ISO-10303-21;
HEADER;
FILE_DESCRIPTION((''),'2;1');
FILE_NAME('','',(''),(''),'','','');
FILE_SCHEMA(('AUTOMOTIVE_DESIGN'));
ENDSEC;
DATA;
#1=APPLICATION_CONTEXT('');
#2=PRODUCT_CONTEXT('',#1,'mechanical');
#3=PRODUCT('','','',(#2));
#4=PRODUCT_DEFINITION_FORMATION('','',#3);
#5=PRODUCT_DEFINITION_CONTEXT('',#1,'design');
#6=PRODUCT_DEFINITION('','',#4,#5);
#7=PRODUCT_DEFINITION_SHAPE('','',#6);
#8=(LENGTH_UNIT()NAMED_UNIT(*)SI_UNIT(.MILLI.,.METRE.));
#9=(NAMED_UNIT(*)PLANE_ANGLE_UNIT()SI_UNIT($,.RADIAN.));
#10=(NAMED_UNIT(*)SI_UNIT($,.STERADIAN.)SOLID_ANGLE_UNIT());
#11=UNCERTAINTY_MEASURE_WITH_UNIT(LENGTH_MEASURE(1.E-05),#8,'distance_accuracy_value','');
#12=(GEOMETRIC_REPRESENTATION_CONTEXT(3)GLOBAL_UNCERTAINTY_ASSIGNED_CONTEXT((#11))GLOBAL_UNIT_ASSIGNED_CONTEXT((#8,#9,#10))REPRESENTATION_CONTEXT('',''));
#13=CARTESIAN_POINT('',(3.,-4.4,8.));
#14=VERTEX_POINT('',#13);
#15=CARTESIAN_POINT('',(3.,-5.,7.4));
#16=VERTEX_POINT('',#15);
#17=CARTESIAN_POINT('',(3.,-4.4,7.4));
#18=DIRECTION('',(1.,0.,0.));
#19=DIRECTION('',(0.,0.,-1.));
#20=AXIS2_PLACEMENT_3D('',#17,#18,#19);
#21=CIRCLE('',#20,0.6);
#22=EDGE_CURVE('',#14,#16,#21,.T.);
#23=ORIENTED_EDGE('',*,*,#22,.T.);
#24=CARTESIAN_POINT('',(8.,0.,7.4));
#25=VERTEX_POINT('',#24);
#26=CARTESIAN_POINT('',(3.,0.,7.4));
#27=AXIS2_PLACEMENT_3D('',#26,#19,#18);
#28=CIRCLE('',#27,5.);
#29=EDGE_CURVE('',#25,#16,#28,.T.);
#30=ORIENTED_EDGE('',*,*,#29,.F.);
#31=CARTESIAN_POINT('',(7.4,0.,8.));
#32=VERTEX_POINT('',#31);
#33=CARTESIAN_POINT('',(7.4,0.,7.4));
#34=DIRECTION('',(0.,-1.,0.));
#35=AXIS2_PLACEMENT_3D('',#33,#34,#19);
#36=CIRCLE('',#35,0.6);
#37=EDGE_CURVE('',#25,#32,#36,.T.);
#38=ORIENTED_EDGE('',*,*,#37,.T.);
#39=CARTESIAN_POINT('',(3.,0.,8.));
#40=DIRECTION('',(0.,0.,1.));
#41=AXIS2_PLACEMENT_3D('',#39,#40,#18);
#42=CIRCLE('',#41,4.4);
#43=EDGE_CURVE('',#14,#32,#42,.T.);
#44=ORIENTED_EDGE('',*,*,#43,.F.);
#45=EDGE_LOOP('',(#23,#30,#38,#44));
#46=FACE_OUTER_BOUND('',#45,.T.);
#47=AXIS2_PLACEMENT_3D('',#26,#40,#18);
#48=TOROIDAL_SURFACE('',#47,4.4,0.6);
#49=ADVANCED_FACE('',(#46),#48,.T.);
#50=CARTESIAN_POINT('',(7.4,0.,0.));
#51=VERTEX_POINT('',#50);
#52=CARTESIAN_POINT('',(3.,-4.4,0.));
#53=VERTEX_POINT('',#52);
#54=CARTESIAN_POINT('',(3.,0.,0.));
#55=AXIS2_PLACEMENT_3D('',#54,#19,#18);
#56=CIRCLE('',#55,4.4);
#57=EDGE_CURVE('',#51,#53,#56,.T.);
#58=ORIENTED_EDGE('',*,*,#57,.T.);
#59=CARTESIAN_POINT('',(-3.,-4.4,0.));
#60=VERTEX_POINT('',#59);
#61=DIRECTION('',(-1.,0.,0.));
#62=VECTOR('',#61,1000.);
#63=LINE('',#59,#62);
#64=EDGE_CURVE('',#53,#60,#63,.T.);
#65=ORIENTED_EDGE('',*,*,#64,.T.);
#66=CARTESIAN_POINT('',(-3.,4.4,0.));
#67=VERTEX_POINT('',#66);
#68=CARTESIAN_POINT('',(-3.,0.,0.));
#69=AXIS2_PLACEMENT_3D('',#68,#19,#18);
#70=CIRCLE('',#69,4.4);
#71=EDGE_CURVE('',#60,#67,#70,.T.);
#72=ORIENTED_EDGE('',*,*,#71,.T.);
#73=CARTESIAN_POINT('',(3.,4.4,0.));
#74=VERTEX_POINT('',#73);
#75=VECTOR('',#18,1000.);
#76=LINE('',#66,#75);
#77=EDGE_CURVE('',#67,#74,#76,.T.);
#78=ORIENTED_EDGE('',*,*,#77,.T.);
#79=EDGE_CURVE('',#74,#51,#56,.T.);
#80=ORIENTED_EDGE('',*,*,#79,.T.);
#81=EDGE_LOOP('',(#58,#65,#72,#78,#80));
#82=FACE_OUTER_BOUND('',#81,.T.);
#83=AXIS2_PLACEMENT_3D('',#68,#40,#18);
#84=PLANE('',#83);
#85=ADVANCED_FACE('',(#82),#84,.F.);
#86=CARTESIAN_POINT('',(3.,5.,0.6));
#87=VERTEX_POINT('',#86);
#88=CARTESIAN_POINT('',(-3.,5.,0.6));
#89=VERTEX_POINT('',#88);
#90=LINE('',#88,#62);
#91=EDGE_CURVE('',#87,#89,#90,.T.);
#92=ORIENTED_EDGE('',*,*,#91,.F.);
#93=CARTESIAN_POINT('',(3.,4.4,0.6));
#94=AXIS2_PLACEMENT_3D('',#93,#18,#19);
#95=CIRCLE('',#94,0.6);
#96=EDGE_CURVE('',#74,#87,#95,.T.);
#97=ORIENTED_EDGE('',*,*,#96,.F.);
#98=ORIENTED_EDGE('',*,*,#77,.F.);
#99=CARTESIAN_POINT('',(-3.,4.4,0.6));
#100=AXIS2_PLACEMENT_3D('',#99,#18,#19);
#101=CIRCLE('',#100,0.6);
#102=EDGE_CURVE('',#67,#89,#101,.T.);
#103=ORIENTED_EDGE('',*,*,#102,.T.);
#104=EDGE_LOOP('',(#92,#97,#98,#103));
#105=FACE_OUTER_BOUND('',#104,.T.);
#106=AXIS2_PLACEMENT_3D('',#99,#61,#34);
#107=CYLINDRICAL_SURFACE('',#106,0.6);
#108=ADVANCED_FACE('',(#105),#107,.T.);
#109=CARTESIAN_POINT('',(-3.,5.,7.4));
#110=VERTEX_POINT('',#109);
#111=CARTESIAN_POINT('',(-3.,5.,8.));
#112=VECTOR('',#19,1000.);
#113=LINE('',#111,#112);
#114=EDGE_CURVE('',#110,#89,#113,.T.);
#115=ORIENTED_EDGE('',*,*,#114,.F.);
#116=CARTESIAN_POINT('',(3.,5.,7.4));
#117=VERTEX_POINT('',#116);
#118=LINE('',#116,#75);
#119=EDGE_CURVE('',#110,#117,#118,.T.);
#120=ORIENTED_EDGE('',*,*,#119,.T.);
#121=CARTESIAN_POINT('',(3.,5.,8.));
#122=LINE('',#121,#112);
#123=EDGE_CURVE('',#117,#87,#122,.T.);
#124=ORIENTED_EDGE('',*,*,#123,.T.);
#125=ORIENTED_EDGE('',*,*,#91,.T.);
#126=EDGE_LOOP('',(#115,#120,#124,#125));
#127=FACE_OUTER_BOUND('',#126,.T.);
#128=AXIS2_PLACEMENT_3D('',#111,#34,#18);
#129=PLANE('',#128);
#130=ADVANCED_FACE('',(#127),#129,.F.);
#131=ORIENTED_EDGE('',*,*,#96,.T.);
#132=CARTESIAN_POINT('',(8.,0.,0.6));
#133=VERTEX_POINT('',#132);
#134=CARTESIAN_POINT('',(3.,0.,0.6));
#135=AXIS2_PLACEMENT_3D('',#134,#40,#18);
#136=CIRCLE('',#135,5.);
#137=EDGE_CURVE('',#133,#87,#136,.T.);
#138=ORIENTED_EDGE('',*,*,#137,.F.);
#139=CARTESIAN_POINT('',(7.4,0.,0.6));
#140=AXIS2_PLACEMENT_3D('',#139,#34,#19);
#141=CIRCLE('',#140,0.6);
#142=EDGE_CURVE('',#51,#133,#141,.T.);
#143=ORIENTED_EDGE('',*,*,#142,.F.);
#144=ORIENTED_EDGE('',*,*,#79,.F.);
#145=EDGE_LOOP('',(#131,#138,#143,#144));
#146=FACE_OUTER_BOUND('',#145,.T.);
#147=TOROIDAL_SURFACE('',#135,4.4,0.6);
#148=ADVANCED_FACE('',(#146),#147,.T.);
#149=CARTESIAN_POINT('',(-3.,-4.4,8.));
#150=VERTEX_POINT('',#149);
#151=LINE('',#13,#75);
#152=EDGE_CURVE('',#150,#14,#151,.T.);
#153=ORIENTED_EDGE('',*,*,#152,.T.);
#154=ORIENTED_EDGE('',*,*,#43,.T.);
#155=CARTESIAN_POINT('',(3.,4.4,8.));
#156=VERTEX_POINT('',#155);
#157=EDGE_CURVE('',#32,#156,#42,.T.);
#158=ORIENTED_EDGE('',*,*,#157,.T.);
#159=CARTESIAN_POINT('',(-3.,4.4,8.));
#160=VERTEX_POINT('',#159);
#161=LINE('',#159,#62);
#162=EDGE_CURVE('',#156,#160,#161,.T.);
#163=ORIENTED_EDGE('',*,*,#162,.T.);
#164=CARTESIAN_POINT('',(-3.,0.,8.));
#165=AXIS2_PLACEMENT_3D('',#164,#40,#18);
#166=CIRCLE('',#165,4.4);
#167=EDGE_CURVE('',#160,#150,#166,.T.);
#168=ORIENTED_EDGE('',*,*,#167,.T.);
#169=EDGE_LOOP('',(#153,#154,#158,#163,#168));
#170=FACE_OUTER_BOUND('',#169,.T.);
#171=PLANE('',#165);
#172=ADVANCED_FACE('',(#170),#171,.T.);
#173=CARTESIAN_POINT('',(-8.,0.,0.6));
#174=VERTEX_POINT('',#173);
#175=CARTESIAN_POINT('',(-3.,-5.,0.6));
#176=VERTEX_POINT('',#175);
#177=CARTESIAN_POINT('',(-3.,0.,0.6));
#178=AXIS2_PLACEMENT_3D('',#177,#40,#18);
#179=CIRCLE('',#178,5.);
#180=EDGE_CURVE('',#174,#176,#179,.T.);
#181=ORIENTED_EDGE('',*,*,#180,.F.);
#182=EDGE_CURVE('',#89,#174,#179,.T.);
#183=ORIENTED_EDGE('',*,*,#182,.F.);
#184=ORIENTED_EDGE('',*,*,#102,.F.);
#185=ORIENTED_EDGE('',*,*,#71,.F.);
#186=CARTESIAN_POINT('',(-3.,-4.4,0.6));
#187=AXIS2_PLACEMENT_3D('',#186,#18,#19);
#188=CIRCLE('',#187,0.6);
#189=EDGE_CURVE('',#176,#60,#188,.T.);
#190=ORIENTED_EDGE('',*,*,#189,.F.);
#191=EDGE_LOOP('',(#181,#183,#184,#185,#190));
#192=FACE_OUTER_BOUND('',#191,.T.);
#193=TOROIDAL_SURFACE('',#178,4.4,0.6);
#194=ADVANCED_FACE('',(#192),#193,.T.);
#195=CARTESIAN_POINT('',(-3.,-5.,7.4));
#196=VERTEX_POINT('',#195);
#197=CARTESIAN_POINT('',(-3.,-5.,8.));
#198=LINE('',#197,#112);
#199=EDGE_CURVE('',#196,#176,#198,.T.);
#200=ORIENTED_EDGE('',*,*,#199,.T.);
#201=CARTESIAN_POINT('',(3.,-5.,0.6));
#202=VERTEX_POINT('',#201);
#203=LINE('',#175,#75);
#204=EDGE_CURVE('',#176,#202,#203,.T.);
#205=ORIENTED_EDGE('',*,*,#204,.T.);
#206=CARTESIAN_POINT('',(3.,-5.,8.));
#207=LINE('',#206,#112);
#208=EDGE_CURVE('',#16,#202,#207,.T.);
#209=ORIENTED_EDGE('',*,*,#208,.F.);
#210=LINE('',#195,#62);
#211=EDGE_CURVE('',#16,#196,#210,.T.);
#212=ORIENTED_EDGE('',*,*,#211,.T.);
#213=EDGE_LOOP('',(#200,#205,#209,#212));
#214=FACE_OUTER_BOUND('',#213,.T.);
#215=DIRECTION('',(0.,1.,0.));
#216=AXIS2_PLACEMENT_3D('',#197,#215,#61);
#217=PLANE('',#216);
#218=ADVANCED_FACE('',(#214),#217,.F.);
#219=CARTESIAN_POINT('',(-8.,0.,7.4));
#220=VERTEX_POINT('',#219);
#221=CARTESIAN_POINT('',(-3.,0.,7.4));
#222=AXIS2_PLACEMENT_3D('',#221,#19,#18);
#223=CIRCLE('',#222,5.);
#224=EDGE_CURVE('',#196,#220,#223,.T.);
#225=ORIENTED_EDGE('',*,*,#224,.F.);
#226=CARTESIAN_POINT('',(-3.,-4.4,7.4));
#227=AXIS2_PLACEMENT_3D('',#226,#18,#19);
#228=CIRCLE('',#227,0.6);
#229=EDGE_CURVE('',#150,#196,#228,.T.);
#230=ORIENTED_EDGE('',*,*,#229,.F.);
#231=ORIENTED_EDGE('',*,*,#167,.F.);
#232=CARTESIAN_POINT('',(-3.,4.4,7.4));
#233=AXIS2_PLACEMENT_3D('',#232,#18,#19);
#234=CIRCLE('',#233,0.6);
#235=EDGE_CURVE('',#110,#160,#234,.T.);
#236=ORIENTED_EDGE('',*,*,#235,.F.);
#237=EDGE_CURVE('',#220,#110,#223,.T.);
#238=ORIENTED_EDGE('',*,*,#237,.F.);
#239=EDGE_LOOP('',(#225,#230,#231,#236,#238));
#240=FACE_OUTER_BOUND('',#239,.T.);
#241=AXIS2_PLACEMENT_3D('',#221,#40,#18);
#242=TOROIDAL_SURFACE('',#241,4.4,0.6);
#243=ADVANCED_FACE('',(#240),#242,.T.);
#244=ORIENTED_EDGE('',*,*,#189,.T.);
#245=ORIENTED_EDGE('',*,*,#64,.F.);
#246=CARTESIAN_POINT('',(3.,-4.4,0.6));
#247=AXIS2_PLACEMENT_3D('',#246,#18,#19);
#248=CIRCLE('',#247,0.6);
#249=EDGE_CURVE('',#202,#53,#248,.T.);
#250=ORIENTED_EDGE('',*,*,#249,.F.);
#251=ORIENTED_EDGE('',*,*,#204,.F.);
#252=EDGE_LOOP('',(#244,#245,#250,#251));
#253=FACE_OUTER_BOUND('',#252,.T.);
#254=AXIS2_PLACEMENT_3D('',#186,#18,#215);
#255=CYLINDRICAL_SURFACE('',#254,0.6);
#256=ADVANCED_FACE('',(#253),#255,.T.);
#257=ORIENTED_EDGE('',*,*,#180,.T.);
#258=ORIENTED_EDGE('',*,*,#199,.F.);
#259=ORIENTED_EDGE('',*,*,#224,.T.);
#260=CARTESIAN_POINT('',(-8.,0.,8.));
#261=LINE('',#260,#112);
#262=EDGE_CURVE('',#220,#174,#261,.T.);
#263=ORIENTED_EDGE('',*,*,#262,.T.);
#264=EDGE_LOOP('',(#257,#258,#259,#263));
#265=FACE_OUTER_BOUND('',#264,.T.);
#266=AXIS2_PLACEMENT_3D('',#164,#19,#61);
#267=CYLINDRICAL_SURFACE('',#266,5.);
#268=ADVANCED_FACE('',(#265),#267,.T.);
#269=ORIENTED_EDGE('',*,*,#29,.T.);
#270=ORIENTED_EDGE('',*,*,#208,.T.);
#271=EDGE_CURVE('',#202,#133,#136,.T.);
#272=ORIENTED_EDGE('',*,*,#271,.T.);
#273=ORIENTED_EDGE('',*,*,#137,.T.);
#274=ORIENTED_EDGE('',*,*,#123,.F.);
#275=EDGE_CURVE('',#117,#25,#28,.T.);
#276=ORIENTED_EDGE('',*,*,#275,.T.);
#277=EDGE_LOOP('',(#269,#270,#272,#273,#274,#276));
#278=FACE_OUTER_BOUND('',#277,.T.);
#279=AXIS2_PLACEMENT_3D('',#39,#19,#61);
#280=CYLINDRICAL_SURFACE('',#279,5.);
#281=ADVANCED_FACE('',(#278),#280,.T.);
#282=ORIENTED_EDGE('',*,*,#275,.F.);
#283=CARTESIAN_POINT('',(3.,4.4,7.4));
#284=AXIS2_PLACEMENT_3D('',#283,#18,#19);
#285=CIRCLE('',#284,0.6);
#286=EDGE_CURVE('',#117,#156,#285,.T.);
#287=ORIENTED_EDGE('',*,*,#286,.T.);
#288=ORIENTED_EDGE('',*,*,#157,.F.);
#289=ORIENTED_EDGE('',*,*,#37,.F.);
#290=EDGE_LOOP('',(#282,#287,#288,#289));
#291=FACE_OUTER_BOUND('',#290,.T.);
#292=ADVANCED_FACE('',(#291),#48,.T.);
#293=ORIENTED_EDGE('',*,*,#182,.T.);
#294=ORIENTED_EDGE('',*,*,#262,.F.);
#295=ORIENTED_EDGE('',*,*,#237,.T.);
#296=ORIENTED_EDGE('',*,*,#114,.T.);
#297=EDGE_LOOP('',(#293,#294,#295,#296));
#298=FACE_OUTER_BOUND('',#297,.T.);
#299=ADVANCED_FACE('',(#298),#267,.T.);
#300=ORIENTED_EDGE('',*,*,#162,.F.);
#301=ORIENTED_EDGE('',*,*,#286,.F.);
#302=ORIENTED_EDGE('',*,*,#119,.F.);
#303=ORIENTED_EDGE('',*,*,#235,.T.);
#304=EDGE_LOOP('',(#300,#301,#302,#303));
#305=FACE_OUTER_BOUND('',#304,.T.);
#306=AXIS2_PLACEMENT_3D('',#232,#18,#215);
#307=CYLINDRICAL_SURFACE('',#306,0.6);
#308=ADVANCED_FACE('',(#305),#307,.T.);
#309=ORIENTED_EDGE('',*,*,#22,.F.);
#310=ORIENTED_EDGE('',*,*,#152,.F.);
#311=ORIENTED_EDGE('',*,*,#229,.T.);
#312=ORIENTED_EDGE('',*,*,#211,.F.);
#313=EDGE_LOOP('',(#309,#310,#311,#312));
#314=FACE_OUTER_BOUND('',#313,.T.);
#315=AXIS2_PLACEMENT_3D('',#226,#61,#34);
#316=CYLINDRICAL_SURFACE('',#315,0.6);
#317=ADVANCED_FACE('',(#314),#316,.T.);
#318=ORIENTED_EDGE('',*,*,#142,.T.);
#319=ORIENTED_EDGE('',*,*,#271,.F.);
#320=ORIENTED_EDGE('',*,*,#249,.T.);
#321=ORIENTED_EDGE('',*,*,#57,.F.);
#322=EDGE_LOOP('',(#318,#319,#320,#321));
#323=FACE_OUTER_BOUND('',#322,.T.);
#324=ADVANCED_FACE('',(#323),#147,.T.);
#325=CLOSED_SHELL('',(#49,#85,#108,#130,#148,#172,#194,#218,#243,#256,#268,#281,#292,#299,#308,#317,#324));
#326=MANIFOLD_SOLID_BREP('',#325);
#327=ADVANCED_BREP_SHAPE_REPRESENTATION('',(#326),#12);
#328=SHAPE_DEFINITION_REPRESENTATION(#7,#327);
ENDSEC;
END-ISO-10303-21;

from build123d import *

# Parameters (mm, degrees)
EXTRUDE_523_DEPTH = 8
FILLET_1_R        = 0.6


with BuildPart() as part:
    # 草图1 → Extrude 523 (new body)
    with BuildSketch(Plane.XY):
        with BuildLine():
            Line((-3, 5), (3, 5))
            ThreePointArc((3, 5), (8, 0), (3, -5))
            Line((3, -5), (-3, -5))
            ThreePointArc((-3, -5), (-8, 0), (-3, 5))
        make_face()
    extrude(amount=EXTRUDE_523_DEPTH)

    # 圆角1
    fillet_1_edges = [part.edges().sort_by_distance(p)[0] for p in [
        (8, 0, 8),
        (0, 5, 8),
        (-8, 0, 8),
        (0, 5, 0),
        (8, 0, 0),
        (0, -5, 0),
        (-8, 0, 0),
        (0, -5, 8),
    ]]
    fillet(fillet_1_edges, radius=FILLET_1_R)


solid = part.part
